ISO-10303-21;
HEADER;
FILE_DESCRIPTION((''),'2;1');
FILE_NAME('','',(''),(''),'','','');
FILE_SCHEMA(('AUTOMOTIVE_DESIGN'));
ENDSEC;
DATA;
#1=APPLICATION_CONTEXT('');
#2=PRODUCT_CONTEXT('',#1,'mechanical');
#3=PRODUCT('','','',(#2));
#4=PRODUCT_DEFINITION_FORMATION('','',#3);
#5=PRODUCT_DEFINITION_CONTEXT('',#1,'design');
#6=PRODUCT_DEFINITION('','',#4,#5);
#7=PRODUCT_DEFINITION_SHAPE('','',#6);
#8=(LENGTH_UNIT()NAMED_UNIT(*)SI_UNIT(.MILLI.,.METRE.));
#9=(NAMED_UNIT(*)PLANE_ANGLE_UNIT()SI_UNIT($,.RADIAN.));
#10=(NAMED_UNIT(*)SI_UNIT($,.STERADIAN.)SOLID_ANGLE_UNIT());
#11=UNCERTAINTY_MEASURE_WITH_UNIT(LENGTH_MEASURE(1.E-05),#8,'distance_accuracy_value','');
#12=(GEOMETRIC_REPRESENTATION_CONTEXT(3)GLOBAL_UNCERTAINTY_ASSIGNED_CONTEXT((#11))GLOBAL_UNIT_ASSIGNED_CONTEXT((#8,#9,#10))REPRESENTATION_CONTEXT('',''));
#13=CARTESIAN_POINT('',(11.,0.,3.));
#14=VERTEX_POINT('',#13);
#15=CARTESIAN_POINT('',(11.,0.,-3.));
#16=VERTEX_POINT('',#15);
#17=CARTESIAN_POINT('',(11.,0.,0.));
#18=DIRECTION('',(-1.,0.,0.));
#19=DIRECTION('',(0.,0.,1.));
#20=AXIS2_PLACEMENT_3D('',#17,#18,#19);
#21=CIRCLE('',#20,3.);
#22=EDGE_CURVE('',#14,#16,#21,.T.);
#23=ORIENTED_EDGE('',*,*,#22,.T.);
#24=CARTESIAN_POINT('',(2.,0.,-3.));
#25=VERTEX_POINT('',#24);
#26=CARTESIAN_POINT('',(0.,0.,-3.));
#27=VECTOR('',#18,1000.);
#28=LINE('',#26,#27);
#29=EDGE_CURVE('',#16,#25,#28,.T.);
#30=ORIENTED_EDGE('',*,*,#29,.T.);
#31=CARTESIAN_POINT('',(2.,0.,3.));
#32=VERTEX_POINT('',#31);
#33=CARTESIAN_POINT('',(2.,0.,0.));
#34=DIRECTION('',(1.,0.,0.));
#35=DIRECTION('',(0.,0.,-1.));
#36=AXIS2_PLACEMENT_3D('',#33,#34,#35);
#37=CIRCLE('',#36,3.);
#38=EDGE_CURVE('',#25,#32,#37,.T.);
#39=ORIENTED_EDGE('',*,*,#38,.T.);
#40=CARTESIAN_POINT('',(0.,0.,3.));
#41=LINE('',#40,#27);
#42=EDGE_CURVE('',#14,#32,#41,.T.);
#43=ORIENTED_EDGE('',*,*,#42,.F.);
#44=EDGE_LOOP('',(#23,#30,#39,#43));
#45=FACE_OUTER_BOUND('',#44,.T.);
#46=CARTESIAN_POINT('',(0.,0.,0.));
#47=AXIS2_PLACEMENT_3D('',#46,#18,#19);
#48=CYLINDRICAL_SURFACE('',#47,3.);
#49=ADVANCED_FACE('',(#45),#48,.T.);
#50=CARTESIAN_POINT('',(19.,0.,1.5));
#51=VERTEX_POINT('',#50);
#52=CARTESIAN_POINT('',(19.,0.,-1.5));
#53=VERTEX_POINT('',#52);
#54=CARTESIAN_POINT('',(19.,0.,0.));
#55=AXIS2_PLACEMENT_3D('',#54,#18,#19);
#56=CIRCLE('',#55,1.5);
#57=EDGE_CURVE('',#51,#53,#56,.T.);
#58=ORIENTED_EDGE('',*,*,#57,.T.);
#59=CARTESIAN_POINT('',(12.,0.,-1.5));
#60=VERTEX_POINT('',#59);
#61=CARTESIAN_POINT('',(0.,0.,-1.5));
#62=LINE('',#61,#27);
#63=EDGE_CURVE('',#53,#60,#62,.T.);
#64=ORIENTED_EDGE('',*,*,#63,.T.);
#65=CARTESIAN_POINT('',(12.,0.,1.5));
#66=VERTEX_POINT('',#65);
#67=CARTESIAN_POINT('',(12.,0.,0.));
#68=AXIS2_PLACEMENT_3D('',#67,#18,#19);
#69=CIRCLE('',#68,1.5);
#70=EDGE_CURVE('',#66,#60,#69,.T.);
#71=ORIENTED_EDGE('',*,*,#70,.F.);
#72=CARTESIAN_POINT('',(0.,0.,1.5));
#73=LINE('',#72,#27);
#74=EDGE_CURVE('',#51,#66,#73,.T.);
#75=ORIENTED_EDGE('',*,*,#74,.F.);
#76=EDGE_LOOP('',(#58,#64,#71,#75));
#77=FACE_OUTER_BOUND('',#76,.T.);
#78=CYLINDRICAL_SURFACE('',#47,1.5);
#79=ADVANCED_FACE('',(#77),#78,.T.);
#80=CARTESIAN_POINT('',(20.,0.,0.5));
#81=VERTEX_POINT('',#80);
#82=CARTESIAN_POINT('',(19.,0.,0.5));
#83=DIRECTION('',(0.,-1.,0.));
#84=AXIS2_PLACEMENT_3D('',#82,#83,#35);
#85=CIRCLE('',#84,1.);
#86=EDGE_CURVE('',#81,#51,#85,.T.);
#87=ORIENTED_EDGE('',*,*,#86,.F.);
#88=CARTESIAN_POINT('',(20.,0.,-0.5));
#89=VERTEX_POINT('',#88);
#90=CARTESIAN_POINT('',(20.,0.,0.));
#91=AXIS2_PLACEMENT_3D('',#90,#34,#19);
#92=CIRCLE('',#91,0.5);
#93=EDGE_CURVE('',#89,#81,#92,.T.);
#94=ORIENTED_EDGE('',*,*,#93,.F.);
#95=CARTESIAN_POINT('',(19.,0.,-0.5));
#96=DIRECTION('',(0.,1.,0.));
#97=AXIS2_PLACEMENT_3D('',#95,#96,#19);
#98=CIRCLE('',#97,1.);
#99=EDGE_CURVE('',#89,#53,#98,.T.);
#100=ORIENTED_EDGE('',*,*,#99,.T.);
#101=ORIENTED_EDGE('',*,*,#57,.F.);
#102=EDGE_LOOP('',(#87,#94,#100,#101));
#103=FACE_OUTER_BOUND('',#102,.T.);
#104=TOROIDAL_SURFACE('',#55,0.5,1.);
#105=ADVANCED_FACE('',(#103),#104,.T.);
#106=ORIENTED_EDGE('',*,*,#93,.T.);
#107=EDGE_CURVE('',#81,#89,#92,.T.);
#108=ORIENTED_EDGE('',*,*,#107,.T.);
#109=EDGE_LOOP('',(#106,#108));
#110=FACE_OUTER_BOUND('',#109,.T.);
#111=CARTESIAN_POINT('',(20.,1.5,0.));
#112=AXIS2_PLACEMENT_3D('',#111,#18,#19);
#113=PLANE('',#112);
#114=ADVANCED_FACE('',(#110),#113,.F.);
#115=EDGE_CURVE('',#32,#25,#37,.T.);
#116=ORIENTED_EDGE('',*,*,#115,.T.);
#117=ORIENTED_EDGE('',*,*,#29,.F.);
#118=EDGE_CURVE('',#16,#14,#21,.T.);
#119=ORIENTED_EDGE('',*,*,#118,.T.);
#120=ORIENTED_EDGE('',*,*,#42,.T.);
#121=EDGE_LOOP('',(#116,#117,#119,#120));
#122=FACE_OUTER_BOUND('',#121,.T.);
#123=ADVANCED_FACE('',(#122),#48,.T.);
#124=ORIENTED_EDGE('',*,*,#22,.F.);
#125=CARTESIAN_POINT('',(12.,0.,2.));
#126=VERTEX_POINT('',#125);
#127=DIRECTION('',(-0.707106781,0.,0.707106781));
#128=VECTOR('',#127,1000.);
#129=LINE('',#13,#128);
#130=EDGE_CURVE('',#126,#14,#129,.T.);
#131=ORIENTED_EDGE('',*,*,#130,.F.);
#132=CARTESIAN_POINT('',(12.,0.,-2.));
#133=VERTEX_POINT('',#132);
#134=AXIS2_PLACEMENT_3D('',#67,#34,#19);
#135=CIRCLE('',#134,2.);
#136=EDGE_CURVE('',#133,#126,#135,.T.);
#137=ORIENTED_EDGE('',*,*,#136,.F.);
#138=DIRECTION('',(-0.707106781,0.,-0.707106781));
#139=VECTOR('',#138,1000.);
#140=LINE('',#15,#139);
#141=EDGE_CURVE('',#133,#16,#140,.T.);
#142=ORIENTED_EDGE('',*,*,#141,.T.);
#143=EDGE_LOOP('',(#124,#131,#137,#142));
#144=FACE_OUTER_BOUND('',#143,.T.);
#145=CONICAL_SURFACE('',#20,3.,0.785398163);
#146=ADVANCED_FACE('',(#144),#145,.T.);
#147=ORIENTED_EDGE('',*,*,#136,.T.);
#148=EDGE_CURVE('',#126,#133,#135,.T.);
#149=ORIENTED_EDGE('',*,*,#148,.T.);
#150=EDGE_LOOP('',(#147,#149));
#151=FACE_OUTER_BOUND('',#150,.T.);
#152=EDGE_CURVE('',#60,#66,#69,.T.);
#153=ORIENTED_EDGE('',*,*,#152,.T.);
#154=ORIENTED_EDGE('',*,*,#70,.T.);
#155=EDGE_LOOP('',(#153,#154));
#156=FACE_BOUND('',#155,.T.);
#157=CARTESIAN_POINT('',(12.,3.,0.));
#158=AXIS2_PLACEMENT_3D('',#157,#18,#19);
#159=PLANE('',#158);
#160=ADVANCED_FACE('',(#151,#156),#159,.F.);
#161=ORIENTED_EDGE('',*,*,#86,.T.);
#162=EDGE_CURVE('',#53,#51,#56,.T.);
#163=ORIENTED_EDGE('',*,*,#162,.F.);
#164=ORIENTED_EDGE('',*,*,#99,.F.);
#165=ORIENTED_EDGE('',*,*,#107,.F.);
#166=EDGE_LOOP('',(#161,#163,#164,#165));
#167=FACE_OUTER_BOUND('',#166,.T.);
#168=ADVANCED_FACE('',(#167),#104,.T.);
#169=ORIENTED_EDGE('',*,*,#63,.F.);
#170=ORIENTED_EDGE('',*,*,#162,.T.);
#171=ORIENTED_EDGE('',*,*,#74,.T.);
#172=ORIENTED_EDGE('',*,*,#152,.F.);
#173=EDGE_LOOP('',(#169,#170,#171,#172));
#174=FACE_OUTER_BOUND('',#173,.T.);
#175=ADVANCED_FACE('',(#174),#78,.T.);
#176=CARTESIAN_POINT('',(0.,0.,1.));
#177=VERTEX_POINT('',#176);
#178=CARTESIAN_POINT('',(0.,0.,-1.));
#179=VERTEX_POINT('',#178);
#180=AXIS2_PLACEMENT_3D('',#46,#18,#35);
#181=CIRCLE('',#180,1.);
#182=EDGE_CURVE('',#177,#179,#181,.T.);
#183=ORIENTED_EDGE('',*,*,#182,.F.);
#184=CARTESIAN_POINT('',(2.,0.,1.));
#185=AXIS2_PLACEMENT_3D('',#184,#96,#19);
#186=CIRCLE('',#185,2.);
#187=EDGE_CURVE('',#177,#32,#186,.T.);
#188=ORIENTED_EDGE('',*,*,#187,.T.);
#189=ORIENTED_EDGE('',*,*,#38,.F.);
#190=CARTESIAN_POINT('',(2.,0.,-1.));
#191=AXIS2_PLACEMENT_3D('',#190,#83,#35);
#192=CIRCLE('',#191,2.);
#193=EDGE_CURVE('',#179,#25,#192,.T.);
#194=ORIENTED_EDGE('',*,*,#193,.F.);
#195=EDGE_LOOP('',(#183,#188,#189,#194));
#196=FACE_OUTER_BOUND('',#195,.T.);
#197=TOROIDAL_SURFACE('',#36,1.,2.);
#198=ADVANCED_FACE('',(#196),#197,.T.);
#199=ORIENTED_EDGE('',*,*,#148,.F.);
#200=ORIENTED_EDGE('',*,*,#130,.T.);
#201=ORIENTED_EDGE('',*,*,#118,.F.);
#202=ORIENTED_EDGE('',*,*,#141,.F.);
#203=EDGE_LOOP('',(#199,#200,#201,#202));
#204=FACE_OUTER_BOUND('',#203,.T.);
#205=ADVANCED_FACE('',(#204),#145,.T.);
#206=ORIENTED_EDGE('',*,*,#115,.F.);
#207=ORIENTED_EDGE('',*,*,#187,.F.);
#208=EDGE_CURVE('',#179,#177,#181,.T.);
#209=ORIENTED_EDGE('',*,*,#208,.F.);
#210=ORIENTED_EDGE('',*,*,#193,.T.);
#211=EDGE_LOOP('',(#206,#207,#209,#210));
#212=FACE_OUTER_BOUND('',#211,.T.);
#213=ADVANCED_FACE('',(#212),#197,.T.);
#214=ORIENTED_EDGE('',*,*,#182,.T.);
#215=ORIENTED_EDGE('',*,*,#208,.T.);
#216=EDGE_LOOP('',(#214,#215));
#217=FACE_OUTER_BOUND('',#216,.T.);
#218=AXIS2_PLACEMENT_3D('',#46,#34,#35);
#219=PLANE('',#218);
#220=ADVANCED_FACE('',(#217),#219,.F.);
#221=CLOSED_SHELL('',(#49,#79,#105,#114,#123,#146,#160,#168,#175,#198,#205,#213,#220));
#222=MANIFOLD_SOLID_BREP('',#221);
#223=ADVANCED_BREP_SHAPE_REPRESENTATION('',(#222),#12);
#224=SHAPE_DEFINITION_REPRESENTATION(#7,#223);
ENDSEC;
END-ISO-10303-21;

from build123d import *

# Parameters (mm, degrees)
FILLET1_R     = 2
FILLET2_R     = 1
CHAMFER1_SIZE = 1


with BuildPart() as part:
    # Sketch1 → Revolve1 (revolve)
    with BuildSketch(Plane.XY, mode=Mode.PRIVATE) as revolve1_sk:
        Polygon((0, 0), (0, 3), (12, 3), (12, 1.5), (20, 1.5), (20, 0), align=None)
    revolve(revolve1_sk.sketch.rotate(Axis((0, 0, 0), (1, 0, 0)), 90), axis=Axis((0, 0, 0), (1, 0, 0)))

    # Fillet1
    fillet1_edges = [part.edges().sort_by_distance(p)[0] for p in [
        (0, 0, -3),
    ]]
    fillet(fillet1_edges, radius=FILLET1_R)

    # Fillet2
    fillet2_edges = [part.edges().sort_by_distance(p)[0] for p in [
        (20, 0, -1.5),
    ]]
    fillet(fillet2_edges, radius=FILLET2_R)

    # Chamfer1
    chamfer1_edges = [part.edges().sort_by_distance(p)[0] for p in [
        (12, 0, -3),
    ]]
    chamfer(chamfer1_edges, length=CHAMFER1_SIZE)


solid = part.part
